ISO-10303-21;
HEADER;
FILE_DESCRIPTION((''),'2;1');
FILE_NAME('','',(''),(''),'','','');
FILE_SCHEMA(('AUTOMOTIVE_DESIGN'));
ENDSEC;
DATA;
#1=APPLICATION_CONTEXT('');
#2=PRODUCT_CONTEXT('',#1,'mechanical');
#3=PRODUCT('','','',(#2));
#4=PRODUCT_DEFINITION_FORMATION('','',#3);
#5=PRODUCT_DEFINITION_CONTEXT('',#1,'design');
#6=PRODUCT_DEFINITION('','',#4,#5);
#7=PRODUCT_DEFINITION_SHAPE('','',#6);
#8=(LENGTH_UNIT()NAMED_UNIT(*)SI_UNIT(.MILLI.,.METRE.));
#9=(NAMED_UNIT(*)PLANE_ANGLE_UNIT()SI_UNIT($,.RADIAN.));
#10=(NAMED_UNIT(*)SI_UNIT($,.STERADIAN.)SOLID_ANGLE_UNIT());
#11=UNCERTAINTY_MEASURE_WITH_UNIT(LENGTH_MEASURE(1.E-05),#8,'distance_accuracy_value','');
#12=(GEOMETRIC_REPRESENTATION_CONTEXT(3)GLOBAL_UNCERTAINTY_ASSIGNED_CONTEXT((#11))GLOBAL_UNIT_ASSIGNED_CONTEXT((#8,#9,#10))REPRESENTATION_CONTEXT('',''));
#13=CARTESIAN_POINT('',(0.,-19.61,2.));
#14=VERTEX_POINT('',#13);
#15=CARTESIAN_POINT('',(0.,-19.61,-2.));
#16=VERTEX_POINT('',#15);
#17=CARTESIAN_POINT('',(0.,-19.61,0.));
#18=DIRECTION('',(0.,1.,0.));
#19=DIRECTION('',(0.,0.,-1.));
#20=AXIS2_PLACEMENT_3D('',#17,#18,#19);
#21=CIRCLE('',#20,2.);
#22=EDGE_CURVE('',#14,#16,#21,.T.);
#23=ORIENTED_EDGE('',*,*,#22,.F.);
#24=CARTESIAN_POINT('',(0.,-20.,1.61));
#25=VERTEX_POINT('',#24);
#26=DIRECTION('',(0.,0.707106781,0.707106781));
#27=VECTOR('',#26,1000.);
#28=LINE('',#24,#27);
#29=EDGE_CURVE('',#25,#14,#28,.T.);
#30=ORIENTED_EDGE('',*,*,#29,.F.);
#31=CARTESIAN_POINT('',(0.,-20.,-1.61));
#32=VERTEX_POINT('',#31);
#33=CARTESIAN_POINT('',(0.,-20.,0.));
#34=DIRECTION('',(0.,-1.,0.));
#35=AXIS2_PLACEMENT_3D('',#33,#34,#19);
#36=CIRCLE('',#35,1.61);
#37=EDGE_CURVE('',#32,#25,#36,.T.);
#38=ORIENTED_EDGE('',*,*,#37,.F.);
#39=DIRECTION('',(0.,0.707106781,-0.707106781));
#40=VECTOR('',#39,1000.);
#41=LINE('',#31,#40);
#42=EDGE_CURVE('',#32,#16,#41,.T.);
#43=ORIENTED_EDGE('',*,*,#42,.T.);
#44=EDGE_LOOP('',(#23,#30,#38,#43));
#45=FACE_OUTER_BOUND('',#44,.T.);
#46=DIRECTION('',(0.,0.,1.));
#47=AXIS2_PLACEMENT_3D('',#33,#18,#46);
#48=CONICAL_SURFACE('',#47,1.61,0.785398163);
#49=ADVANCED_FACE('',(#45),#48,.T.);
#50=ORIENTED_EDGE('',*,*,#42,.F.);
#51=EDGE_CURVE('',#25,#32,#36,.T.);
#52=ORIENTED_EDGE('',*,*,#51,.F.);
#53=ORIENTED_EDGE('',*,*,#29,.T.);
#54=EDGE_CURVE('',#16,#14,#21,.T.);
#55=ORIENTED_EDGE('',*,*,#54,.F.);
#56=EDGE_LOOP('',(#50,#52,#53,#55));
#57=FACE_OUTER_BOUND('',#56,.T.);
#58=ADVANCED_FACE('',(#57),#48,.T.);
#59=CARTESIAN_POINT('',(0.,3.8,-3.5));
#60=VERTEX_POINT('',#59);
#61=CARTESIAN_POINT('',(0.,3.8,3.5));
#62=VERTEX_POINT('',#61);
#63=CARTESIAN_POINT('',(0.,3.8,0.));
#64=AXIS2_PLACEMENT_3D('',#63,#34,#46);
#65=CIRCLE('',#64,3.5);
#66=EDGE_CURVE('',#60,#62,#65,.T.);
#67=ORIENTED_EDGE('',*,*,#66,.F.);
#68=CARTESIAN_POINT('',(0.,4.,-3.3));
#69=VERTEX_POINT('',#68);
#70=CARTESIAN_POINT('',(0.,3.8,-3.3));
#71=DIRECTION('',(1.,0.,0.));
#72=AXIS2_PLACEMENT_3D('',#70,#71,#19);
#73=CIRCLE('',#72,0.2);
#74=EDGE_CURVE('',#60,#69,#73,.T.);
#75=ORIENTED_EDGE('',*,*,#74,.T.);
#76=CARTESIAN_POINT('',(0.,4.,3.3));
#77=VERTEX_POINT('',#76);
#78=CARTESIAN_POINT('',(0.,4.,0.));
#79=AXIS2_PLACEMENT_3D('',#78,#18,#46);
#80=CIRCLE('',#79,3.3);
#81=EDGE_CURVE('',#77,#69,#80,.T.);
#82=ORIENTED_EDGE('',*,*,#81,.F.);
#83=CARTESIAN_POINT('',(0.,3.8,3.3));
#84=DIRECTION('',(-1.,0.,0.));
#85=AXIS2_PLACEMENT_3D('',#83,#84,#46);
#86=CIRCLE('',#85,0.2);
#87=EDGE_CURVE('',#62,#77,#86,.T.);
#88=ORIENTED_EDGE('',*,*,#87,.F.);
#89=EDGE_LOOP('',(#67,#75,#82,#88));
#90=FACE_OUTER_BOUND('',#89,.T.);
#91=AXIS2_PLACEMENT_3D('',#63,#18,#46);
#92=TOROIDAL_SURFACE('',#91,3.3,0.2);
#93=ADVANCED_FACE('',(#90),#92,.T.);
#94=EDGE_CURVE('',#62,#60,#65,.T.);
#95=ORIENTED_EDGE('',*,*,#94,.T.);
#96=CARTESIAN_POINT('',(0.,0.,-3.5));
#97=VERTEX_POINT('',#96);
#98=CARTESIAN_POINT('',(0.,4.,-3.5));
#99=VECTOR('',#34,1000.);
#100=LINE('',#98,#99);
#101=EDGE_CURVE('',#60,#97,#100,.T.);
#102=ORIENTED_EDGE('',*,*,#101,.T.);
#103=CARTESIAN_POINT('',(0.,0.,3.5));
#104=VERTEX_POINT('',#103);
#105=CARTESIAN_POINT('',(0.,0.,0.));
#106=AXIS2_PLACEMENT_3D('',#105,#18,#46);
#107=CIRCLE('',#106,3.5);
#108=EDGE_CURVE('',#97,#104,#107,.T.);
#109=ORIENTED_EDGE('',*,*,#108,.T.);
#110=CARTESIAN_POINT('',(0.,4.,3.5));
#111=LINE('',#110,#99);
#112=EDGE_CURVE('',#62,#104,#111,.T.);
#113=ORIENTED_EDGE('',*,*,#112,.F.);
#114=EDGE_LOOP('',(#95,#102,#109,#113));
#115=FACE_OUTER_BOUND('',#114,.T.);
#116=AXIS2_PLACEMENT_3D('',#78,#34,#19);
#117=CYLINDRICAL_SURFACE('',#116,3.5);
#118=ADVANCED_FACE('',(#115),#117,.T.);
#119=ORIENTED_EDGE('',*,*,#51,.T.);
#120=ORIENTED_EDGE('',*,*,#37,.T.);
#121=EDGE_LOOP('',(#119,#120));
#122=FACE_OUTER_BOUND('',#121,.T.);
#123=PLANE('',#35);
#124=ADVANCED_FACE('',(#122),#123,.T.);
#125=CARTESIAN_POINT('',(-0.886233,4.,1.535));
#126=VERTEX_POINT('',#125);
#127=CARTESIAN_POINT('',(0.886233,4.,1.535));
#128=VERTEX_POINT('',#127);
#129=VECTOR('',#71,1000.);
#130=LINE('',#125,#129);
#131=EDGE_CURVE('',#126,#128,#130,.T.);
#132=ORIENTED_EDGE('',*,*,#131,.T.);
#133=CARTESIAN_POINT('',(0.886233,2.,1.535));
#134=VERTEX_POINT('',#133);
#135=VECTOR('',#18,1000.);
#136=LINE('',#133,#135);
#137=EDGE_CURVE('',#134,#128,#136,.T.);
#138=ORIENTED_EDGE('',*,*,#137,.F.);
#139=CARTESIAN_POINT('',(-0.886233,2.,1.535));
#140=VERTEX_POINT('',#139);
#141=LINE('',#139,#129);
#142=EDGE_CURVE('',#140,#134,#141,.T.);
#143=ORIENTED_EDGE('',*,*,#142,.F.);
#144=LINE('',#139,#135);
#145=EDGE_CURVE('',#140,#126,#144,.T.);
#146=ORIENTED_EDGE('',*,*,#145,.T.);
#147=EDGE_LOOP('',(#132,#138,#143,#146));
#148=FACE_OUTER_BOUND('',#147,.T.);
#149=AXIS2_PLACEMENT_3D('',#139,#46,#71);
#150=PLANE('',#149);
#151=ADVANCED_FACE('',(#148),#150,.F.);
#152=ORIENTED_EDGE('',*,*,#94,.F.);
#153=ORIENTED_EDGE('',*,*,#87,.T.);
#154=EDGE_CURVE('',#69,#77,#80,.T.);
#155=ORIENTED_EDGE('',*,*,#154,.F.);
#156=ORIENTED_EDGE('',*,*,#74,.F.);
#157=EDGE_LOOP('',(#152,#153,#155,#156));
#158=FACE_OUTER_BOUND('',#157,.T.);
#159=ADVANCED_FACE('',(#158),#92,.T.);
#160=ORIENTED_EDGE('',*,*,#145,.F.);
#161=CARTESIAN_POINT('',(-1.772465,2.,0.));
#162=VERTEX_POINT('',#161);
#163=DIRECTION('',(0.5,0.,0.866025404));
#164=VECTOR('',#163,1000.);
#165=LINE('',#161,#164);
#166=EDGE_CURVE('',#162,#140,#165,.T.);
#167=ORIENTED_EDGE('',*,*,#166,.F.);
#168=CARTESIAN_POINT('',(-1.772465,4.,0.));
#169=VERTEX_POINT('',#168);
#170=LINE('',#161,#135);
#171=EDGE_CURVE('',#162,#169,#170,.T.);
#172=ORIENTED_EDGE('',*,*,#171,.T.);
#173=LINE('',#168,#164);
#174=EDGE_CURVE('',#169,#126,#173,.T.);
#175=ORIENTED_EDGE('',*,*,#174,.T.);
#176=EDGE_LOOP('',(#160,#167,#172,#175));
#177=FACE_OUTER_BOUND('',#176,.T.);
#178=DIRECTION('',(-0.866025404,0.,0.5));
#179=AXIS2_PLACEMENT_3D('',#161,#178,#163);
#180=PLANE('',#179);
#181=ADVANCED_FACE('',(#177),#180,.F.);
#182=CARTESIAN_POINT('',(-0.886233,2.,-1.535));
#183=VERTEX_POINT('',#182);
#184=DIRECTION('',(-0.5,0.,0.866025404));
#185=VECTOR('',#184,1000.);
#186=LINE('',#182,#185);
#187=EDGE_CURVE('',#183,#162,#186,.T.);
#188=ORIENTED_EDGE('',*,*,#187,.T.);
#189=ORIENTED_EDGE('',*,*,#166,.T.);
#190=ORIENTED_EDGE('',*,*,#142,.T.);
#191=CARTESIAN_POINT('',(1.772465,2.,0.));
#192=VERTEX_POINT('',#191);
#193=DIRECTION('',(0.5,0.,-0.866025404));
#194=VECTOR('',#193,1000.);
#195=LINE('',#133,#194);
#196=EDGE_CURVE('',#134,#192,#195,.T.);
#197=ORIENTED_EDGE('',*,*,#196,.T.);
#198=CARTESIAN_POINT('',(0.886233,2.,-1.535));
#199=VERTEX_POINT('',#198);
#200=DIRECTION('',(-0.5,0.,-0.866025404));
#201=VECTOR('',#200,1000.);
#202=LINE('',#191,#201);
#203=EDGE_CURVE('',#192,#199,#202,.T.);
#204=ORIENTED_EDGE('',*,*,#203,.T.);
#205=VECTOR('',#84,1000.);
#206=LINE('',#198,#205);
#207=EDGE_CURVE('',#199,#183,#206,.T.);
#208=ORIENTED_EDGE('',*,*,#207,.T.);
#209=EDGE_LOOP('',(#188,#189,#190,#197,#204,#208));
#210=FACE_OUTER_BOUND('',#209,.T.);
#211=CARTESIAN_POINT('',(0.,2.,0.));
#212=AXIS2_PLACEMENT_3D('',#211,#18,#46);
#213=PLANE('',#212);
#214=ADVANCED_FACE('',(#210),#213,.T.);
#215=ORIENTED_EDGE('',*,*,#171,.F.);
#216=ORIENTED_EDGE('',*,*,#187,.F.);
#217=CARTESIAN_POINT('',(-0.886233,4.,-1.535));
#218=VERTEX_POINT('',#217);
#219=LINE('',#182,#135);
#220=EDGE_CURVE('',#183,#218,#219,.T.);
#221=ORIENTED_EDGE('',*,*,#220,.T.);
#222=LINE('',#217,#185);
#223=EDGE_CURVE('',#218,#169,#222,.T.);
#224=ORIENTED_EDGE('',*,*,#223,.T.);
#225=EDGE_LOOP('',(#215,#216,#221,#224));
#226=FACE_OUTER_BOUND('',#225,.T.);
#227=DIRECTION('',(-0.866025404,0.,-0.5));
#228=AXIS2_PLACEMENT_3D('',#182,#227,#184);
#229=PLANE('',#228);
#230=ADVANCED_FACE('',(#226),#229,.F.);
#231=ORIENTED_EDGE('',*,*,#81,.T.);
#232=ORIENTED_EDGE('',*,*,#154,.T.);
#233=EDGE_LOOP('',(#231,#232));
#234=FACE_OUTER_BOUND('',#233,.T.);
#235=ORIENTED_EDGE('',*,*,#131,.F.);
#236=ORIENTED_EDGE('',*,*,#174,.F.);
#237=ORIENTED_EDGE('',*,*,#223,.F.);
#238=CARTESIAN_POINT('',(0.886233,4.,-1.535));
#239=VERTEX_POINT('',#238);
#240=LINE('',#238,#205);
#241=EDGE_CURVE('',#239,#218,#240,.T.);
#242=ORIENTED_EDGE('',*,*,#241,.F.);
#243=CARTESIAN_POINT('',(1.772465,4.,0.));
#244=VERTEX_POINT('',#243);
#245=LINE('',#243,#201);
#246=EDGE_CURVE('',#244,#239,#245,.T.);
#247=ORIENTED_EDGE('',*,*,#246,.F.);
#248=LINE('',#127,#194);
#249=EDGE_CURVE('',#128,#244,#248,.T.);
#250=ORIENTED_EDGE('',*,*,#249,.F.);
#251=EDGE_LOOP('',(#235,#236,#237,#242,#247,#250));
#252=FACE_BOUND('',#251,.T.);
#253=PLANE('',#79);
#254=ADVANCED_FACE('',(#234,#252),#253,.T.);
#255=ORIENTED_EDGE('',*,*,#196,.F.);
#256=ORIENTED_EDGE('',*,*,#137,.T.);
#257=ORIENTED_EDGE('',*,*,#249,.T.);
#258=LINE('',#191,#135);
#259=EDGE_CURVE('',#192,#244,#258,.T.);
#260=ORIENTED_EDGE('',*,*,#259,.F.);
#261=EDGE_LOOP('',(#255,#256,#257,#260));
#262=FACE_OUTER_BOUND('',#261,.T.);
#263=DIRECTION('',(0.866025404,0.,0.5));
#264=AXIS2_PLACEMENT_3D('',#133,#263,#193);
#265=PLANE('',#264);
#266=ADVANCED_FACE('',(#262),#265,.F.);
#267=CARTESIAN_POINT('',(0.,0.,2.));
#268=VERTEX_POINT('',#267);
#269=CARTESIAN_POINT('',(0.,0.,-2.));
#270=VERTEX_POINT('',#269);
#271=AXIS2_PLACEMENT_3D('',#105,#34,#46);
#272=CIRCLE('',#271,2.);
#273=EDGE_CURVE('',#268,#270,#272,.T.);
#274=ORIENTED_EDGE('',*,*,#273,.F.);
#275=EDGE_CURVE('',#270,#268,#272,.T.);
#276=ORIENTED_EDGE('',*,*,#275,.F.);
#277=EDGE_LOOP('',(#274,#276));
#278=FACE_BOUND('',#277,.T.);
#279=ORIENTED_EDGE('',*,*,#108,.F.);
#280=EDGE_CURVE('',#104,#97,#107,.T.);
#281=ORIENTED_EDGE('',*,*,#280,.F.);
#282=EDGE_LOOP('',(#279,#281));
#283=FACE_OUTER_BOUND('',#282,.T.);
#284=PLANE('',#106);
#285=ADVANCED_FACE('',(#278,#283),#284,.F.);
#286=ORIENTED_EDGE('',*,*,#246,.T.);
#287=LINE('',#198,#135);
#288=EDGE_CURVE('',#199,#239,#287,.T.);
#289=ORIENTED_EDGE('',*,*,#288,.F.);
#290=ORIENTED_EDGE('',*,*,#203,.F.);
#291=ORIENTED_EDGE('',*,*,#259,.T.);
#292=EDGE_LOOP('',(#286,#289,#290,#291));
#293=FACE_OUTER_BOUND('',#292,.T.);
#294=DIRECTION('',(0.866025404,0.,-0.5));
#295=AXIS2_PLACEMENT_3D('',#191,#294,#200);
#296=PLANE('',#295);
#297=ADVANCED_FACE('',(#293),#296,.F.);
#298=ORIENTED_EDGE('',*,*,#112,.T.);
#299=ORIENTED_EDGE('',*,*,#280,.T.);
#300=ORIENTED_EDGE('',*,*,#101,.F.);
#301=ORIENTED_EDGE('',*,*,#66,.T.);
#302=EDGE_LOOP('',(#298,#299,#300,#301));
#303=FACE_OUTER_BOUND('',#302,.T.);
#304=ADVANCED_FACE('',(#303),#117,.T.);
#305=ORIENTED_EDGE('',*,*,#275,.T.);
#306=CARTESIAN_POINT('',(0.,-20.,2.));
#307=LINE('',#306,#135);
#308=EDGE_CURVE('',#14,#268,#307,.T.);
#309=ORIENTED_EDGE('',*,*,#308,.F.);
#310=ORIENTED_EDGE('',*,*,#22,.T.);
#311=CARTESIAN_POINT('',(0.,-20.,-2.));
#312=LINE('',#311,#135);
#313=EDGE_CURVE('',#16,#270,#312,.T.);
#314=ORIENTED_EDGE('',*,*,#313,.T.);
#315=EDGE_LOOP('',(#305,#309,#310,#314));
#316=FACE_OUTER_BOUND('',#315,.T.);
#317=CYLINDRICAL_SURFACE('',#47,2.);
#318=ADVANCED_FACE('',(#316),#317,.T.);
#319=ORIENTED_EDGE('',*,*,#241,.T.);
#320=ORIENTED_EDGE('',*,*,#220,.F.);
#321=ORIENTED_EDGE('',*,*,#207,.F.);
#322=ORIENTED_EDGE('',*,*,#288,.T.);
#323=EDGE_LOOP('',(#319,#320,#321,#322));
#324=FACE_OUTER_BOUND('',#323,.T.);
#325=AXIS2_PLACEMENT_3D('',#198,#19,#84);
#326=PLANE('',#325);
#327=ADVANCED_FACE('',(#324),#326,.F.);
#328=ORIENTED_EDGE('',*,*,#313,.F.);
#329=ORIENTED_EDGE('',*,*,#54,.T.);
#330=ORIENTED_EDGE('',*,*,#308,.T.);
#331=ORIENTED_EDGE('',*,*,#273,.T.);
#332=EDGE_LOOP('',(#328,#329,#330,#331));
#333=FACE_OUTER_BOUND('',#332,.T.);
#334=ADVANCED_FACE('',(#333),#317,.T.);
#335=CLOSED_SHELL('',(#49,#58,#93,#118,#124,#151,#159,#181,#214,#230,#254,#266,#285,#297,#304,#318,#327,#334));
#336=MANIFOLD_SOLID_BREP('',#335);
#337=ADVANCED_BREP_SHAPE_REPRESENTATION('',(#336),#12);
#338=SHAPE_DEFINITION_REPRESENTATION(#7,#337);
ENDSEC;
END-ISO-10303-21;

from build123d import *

# Parameters (mm, degrees)
SKETCH_1_R          = 3.5
EXTRUDE_1_DEPTH     = 4
CUT_EXTRUDE_1_DEPTH = 2
FILLET_1_R          = 0.2
SKETCH_5_R          = 2
EXTRUDE_2_DEPTH     = 20
CHAMFER_2_SIZE      = 0.39


with BuildPart() as part:
    # 草图1 → 凸台-拉伸1 (new body)
    with BuildSketch(Plane(origin=(0, 0, 0), x_dir=(1, 0, 0), z_dir=(0, 1, 0))):
        with Locations(Location((0, 0, 0), (0, 0, 270))):
            Circle(SKETCH_1_R)
    extrude(amount=EXTRUDE_1_DEPTH)

    # 草图2 → 切除-拉伸1 (cut)
    with BuildSketch(Plane(origin=(0, 4, 0), x_dir=(1, 0, 0), z_dir=(0, 1, 0))):
        Polygon((1.772465326, 0), (0.886232663, 1.535), (-0.886232663, 1.535), (-1.772465326, 0), (-0.886232663, -1.535), (0.886232663, -1.535), align=None)
    extrude(amount=-CUT_EXTRUDE_1_DEPTH, mode=Mode.SUBTRACT)

    # 圆角1
    fillet_1_edges = [part.edges().sort_by_distance(p)[0] for p in [
        (0, 4, -3.5),
    ]]
    fillet(fillet_1_edges, radius=FILLET_1_R)

    # 草图5 → 凸台-拉伸2 (add)
    with BuildSketch(Plane.XZ):
        with Locations(Location((0, 0, 0), (0, 0, 90))):
            Circle(SKETCH_5_R)
    extrude(amount=EXTRUDE_2_DEPTH)

    # 倒角2
    chamfer_2_edges = [part.edges().sort_by_distance(p)[0] for p in [
        (0, -20, -2),
    ]]
    chamfer(chamfer_2_edges, length=CHAMFER_2_SIZE)


solid = part.part
